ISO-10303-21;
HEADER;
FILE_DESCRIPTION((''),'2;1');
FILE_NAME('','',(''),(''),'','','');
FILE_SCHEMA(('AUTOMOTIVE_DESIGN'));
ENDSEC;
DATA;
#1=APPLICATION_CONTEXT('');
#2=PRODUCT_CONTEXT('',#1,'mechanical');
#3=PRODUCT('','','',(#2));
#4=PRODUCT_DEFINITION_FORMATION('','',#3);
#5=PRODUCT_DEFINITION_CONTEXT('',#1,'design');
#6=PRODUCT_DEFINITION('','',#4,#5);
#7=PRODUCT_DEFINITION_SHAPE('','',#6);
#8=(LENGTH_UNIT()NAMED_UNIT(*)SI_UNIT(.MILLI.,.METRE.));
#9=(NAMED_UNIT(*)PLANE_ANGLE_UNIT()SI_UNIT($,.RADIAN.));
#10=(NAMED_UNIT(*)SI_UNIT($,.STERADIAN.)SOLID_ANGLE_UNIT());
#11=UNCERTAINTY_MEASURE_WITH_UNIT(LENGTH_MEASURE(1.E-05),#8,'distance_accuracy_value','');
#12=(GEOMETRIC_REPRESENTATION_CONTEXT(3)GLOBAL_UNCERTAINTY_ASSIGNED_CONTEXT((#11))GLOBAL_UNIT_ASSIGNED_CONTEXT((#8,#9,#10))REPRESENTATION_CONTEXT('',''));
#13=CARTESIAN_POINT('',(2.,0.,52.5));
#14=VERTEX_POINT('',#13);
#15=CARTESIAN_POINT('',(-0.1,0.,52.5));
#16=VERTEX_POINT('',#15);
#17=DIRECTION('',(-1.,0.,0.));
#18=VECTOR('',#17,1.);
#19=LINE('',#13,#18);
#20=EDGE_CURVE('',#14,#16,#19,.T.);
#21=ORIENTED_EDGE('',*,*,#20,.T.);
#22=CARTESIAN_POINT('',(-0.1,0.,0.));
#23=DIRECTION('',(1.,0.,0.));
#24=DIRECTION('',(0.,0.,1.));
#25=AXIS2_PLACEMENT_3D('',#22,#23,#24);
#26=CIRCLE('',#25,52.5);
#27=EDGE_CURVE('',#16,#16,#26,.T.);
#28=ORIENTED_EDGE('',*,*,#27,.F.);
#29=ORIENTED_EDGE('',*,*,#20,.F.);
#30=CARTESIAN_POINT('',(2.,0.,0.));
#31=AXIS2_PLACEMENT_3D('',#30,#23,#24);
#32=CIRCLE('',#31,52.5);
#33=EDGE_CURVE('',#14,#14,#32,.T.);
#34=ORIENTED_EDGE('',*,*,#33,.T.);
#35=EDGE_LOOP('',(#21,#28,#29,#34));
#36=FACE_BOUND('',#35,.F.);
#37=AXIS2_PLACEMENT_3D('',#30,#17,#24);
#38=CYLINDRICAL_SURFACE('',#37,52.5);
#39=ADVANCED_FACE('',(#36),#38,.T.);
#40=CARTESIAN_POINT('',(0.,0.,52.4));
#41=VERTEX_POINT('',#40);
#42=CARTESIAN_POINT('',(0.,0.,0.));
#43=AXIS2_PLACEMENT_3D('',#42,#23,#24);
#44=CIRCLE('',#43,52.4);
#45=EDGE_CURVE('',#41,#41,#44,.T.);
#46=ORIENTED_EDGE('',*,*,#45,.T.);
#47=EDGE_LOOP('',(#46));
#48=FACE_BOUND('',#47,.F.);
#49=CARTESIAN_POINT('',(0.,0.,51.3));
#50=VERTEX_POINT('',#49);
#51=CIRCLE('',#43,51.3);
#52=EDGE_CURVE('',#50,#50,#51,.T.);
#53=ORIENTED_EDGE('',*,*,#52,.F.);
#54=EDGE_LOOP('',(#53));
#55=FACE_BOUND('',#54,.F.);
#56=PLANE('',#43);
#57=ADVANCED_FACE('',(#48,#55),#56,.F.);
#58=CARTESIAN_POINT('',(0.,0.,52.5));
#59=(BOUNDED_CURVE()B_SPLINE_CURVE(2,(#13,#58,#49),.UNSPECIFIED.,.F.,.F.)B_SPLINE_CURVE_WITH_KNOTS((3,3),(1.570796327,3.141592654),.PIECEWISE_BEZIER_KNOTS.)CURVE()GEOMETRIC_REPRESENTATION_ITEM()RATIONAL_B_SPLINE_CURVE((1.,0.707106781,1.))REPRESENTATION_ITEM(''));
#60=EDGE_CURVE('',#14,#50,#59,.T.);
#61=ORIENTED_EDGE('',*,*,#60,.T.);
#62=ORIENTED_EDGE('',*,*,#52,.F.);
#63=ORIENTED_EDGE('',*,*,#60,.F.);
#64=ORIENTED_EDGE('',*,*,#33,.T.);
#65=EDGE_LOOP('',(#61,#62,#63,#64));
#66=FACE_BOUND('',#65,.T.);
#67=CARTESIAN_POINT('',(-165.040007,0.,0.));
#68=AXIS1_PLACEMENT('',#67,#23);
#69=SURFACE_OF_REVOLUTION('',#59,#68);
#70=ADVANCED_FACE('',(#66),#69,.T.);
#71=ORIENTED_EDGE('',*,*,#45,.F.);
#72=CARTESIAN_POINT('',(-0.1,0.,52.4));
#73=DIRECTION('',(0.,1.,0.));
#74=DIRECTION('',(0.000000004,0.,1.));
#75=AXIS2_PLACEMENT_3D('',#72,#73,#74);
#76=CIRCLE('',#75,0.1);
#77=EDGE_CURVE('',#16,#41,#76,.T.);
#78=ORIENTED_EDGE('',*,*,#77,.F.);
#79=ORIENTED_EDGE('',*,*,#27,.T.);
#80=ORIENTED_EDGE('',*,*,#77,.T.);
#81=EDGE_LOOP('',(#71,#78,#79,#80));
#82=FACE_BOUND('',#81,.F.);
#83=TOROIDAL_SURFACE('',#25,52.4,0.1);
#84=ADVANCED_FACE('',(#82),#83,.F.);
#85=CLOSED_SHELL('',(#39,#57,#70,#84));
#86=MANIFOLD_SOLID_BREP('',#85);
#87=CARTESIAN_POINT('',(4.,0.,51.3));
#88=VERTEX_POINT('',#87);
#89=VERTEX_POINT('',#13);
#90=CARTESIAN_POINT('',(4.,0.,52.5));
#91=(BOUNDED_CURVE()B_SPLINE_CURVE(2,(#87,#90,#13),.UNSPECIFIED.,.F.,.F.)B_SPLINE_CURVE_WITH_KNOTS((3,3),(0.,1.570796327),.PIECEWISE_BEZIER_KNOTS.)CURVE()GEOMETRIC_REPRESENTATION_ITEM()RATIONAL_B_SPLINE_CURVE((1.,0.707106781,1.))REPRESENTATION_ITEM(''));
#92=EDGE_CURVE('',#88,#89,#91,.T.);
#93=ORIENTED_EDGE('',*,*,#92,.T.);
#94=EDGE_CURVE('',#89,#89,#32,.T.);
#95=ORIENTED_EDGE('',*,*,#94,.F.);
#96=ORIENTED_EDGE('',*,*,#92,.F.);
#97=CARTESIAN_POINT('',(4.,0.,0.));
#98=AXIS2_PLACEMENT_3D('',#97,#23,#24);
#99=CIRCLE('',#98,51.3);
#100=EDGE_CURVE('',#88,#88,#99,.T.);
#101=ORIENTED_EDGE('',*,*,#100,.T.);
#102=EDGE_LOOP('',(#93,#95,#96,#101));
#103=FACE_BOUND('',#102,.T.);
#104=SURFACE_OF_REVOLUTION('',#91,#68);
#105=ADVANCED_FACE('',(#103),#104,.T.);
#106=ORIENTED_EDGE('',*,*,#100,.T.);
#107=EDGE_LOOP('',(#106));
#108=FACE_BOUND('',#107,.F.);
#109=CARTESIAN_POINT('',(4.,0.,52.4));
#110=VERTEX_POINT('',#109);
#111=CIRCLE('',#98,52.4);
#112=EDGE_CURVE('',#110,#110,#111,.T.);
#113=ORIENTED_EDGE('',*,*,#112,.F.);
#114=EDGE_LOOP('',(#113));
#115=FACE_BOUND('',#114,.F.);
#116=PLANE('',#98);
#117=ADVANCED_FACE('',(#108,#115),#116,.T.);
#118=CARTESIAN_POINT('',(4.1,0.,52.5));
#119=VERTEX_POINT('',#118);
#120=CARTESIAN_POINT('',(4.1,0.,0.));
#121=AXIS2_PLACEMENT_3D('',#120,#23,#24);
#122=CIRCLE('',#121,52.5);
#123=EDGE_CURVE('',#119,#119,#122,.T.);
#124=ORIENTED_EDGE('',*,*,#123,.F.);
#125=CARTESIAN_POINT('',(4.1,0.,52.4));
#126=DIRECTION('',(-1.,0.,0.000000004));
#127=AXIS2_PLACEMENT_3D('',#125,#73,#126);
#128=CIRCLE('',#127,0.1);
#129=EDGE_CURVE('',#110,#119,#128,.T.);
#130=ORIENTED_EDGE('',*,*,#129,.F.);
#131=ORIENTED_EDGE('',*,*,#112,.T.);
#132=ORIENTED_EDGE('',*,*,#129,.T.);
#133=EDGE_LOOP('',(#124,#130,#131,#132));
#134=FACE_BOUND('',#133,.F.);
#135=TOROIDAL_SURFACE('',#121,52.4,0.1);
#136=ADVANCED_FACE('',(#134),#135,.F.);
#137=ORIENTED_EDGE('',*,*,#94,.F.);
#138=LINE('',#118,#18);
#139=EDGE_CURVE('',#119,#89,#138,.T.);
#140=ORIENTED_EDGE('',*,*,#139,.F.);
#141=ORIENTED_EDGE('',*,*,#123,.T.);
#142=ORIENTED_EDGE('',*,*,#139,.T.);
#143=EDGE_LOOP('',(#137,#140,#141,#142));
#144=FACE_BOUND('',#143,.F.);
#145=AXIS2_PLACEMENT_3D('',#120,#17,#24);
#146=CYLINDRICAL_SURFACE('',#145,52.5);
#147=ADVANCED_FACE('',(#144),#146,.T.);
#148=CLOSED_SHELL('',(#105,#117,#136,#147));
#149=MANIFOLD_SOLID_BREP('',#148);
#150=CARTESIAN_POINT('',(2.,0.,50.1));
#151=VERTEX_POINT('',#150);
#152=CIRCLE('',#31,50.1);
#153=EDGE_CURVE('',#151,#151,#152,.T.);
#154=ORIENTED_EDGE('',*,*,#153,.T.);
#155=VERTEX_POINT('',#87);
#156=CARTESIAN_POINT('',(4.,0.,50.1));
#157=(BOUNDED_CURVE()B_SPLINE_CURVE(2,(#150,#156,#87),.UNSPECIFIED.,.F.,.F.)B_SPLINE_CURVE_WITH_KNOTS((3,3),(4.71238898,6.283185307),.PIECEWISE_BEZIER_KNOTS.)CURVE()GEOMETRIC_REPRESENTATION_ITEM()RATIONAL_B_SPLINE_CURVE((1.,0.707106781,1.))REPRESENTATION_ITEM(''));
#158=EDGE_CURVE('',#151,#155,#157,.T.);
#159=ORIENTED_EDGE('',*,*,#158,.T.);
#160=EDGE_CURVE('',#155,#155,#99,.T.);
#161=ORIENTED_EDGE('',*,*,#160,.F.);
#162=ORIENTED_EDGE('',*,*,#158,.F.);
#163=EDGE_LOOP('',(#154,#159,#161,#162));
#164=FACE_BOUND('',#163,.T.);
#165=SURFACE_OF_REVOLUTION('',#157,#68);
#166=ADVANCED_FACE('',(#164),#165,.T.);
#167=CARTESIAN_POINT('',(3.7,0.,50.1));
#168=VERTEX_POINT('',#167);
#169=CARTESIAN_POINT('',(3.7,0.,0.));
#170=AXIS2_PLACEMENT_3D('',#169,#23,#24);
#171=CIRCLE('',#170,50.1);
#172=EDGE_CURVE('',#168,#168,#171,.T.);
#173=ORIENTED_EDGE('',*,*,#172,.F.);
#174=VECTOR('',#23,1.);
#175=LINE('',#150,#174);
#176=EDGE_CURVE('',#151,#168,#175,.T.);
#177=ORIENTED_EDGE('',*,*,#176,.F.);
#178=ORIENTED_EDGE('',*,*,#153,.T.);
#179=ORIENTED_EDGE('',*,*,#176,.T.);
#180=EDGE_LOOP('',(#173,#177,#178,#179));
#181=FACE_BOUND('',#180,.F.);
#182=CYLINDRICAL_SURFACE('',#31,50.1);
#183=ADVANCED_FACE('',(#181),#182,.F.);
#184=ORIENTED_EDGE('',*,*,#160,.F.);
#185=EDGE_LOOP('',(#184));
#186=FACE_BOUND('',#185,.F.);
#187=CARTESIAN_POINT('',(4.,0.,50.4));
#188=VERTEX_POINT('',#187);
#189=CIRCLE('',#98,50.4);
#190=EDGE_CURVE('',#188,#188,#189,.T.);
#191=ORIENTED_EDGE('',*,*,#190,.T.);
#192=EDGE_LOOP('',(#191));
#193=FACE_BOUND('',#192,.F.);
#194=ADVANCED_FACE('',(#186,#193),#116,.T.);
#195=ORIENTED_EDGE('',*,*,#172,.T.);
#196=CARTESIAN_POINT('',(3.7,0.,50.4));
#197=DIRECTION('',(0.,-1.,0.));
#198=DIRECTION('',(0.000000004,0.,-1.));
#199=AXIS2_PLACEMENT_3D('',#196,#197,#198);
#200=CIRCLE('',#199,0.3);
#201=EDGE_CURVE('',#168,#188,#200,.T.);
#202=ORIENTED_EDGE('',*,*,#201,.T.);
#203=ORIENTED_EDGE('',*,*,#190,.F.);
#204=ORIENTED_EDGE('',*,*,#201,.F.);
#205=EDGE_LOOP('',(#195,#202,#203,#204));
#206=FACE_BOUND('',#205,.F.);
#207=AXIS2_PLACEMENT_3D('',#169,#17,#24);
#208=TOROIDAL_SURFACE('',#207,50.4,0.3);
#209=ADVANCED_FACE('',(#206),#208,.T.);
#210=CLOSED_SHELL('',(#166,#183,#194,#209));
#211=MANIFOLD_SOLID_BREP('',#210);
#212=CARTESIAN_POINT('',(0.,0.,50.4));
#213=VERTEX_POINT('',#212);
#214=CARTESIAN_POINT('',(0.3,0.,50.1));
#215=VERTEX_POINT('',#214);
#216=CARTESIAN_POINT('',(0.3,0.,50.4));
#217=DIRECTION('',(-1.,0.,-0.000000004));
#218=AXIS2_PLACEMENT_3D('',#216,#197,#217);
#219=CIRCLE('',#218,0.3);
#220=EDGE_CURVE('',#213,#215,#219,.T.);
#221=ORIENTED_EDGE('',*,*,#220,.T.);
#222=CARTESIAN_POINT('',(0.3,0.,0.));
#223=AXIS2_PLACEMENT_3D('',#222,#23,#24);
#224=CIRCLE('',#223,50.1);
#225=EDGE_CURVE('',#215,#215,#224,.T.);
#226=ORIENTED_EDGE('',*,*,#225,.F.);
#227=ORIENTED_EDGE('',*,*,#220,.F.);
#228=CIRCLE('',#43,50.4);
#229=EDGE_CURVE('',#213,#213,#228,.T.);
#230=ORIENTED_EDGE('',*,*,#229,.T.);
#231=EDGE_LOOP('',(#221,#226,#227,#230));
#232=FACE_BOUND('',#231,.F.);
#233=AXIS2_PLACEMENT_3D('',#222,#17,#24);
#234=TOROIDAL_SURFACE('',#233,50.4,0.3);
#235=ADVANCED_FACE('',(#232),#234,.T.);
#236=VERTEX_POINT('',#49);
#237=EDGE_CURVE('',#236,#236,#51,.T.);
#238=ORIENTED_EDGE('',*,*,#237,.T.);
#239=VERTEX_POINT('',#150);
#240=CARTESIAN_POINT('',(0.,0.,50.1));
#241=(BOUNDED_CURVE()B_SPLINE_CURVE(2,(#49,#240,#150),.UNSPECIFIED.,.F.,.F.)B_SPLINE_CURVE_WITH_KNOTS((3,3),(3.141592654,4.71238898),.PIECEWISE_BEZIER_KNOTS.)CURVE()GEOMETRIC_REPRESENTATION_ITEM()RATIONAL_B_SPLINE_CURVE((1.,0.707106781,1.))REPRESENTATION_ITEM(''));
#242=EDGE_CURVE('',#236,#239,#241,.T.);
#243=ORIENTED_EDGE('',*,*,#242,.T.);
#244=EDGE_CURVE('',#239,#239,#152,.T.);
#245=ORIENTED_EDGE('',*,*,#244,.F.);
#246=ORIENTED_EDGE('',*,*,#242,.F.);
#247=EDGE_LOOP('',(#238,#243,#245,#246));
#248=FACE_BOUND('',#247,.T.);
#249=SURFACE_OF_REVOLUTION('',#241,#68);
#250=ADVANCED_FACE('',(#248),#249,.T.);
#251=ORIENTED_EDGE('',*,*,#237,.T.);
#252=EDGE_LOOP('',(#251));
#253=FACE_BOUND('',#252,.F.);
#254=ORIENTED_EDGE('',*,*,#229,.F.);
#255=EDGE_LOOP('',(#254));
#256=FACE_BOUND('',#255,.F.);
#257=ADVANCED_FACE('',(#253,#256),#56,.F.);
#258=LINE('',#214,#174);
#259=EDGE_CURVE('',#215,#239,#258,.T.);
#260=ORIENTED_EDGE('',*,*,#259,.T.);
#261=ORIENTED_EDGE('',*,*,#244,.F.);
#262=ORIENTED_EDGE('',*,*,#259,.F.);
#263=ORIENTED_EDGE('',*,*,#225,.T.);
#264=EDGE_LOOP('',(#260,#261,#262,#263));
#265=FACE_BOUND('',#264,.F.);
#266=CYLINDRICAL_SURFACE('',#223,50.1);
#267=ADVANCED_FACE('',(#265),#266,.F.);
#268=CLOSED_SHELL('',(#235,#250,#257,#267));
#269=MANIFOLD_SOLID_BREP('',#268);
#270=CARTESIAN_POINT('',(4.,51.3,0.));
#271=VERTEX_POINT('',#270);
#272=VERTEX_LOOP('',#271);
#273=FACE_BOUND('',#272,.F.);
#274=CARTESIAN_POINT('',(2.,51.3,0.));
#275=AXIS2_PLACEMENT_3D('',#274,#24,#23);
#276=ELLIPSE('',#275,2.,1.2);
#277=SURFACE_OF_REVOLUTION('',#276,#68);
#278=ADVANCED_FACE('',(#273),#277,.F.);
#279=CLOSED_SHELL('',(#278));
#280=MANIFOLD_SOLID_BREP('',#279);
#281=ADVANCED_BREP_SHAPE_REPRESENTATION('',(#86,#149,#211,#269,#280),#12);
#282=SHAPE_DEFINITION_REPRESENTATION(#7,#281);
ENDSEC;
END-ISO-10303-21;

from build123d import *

# Parameters (mm, degrees)
SKETCH_1_RX = 2
SKETCH_1_RY = 1.2


with BuildPart() as part:
    # 草图1 → Revolve 664 (revolve)
    with BuildSketch(Plane.XY):
        with Locations((2, 51.3)):
            Ellipse(SKETCH_1_RX, SKETCH_1_RY)
    revolve(axis=Axis((-165.040006745, 0, 0), (1, 0, 0)))


with BuildPart() as body_2:
    # 草图1<4> → Revolve 698 (revolve)
    with BuildSketch(Plane.XY, mode=Mode.PRIVATE) as revolve_698_sk:
        with BuildLine():
            add(Edge.make_bspline(
                [(0, 51.3), (0, 50.1), (2, 50.1)],
                knots=[3.141592654, 3.141592654, 3.141592654, 4.71238898, 4.71238898, 4.71238898], degree=2, weights=[1, 0.707106781, 1]))
            Line((0, 51.3), (0, 50.4))
            ThreePointArc((0, 50.4), (0.087867966, 50.187867966), (0.3, 50.1))
            Line((0.3, 50.1), (2, 50.1))
        make_face()
        with BuildLine():
            add(Edge.make_bspline(
                [(2, 50.1), (4, 50.1), (4, 51.3)],
                knots=[4.71238898, 4.71238898, 4.71238898, 6.283185307, 6.283185307, 6.283185307], degree=2, weights=[1, 0.707106781, 1]))
            Line((2, 50.1), (3.7, 50.1))
            ThreePointArc((3.7, 50.1), (3.912132034, 50.187867966), (4, 50.4))
            Line((4, 50.4), (4, 51.3))
        make_face()
        with BuildLine():
            Line((4.1, 52.5), (2, 52.5))
            add(Edge.make_bspline(
                [(4, 51.3), (4, 52.5), (2, 52.5)],
                knots=[0, 0, 0, 1.570796327, 1.570796327, 1.570796327], degree=2, weights=[1, 0.707106781, 1]))
            Line((4, 51.3), (4, 52.4))
            ThreePointArc((4, 52.4), (4.029289322, 52.470710678), (4.1, 52.5))
        make_face()
        with BuildLine():
            ThreePointArc((-0.1, 52.5), (-0.029289322, 52.470710678), (0, 52.4))
            Line((0, 52.4), (0, 51.3))
            add(Edge.make_bspline(
                [(2, 52.5), (0, 52.5), (0, 51.3)],
                knots=[1.570796327, 1.570796327, 1.570796327, 3.141592654, 3.141592654, 3.141592654], degree=2, weights=[1, 0.707106781, 1]))
            Line((2, 52.5), (-0.1, 52.5))
        make_face()
    revolve(revolve_698_sk.sketch.rotate(Axis((-165.040006745, 0, 0), (1, 0, 0)), 90), axis=Axis((-165.040006745, 0, 0), (1, 0, 0)))


solid = Compound([part.part, body_2.part])
